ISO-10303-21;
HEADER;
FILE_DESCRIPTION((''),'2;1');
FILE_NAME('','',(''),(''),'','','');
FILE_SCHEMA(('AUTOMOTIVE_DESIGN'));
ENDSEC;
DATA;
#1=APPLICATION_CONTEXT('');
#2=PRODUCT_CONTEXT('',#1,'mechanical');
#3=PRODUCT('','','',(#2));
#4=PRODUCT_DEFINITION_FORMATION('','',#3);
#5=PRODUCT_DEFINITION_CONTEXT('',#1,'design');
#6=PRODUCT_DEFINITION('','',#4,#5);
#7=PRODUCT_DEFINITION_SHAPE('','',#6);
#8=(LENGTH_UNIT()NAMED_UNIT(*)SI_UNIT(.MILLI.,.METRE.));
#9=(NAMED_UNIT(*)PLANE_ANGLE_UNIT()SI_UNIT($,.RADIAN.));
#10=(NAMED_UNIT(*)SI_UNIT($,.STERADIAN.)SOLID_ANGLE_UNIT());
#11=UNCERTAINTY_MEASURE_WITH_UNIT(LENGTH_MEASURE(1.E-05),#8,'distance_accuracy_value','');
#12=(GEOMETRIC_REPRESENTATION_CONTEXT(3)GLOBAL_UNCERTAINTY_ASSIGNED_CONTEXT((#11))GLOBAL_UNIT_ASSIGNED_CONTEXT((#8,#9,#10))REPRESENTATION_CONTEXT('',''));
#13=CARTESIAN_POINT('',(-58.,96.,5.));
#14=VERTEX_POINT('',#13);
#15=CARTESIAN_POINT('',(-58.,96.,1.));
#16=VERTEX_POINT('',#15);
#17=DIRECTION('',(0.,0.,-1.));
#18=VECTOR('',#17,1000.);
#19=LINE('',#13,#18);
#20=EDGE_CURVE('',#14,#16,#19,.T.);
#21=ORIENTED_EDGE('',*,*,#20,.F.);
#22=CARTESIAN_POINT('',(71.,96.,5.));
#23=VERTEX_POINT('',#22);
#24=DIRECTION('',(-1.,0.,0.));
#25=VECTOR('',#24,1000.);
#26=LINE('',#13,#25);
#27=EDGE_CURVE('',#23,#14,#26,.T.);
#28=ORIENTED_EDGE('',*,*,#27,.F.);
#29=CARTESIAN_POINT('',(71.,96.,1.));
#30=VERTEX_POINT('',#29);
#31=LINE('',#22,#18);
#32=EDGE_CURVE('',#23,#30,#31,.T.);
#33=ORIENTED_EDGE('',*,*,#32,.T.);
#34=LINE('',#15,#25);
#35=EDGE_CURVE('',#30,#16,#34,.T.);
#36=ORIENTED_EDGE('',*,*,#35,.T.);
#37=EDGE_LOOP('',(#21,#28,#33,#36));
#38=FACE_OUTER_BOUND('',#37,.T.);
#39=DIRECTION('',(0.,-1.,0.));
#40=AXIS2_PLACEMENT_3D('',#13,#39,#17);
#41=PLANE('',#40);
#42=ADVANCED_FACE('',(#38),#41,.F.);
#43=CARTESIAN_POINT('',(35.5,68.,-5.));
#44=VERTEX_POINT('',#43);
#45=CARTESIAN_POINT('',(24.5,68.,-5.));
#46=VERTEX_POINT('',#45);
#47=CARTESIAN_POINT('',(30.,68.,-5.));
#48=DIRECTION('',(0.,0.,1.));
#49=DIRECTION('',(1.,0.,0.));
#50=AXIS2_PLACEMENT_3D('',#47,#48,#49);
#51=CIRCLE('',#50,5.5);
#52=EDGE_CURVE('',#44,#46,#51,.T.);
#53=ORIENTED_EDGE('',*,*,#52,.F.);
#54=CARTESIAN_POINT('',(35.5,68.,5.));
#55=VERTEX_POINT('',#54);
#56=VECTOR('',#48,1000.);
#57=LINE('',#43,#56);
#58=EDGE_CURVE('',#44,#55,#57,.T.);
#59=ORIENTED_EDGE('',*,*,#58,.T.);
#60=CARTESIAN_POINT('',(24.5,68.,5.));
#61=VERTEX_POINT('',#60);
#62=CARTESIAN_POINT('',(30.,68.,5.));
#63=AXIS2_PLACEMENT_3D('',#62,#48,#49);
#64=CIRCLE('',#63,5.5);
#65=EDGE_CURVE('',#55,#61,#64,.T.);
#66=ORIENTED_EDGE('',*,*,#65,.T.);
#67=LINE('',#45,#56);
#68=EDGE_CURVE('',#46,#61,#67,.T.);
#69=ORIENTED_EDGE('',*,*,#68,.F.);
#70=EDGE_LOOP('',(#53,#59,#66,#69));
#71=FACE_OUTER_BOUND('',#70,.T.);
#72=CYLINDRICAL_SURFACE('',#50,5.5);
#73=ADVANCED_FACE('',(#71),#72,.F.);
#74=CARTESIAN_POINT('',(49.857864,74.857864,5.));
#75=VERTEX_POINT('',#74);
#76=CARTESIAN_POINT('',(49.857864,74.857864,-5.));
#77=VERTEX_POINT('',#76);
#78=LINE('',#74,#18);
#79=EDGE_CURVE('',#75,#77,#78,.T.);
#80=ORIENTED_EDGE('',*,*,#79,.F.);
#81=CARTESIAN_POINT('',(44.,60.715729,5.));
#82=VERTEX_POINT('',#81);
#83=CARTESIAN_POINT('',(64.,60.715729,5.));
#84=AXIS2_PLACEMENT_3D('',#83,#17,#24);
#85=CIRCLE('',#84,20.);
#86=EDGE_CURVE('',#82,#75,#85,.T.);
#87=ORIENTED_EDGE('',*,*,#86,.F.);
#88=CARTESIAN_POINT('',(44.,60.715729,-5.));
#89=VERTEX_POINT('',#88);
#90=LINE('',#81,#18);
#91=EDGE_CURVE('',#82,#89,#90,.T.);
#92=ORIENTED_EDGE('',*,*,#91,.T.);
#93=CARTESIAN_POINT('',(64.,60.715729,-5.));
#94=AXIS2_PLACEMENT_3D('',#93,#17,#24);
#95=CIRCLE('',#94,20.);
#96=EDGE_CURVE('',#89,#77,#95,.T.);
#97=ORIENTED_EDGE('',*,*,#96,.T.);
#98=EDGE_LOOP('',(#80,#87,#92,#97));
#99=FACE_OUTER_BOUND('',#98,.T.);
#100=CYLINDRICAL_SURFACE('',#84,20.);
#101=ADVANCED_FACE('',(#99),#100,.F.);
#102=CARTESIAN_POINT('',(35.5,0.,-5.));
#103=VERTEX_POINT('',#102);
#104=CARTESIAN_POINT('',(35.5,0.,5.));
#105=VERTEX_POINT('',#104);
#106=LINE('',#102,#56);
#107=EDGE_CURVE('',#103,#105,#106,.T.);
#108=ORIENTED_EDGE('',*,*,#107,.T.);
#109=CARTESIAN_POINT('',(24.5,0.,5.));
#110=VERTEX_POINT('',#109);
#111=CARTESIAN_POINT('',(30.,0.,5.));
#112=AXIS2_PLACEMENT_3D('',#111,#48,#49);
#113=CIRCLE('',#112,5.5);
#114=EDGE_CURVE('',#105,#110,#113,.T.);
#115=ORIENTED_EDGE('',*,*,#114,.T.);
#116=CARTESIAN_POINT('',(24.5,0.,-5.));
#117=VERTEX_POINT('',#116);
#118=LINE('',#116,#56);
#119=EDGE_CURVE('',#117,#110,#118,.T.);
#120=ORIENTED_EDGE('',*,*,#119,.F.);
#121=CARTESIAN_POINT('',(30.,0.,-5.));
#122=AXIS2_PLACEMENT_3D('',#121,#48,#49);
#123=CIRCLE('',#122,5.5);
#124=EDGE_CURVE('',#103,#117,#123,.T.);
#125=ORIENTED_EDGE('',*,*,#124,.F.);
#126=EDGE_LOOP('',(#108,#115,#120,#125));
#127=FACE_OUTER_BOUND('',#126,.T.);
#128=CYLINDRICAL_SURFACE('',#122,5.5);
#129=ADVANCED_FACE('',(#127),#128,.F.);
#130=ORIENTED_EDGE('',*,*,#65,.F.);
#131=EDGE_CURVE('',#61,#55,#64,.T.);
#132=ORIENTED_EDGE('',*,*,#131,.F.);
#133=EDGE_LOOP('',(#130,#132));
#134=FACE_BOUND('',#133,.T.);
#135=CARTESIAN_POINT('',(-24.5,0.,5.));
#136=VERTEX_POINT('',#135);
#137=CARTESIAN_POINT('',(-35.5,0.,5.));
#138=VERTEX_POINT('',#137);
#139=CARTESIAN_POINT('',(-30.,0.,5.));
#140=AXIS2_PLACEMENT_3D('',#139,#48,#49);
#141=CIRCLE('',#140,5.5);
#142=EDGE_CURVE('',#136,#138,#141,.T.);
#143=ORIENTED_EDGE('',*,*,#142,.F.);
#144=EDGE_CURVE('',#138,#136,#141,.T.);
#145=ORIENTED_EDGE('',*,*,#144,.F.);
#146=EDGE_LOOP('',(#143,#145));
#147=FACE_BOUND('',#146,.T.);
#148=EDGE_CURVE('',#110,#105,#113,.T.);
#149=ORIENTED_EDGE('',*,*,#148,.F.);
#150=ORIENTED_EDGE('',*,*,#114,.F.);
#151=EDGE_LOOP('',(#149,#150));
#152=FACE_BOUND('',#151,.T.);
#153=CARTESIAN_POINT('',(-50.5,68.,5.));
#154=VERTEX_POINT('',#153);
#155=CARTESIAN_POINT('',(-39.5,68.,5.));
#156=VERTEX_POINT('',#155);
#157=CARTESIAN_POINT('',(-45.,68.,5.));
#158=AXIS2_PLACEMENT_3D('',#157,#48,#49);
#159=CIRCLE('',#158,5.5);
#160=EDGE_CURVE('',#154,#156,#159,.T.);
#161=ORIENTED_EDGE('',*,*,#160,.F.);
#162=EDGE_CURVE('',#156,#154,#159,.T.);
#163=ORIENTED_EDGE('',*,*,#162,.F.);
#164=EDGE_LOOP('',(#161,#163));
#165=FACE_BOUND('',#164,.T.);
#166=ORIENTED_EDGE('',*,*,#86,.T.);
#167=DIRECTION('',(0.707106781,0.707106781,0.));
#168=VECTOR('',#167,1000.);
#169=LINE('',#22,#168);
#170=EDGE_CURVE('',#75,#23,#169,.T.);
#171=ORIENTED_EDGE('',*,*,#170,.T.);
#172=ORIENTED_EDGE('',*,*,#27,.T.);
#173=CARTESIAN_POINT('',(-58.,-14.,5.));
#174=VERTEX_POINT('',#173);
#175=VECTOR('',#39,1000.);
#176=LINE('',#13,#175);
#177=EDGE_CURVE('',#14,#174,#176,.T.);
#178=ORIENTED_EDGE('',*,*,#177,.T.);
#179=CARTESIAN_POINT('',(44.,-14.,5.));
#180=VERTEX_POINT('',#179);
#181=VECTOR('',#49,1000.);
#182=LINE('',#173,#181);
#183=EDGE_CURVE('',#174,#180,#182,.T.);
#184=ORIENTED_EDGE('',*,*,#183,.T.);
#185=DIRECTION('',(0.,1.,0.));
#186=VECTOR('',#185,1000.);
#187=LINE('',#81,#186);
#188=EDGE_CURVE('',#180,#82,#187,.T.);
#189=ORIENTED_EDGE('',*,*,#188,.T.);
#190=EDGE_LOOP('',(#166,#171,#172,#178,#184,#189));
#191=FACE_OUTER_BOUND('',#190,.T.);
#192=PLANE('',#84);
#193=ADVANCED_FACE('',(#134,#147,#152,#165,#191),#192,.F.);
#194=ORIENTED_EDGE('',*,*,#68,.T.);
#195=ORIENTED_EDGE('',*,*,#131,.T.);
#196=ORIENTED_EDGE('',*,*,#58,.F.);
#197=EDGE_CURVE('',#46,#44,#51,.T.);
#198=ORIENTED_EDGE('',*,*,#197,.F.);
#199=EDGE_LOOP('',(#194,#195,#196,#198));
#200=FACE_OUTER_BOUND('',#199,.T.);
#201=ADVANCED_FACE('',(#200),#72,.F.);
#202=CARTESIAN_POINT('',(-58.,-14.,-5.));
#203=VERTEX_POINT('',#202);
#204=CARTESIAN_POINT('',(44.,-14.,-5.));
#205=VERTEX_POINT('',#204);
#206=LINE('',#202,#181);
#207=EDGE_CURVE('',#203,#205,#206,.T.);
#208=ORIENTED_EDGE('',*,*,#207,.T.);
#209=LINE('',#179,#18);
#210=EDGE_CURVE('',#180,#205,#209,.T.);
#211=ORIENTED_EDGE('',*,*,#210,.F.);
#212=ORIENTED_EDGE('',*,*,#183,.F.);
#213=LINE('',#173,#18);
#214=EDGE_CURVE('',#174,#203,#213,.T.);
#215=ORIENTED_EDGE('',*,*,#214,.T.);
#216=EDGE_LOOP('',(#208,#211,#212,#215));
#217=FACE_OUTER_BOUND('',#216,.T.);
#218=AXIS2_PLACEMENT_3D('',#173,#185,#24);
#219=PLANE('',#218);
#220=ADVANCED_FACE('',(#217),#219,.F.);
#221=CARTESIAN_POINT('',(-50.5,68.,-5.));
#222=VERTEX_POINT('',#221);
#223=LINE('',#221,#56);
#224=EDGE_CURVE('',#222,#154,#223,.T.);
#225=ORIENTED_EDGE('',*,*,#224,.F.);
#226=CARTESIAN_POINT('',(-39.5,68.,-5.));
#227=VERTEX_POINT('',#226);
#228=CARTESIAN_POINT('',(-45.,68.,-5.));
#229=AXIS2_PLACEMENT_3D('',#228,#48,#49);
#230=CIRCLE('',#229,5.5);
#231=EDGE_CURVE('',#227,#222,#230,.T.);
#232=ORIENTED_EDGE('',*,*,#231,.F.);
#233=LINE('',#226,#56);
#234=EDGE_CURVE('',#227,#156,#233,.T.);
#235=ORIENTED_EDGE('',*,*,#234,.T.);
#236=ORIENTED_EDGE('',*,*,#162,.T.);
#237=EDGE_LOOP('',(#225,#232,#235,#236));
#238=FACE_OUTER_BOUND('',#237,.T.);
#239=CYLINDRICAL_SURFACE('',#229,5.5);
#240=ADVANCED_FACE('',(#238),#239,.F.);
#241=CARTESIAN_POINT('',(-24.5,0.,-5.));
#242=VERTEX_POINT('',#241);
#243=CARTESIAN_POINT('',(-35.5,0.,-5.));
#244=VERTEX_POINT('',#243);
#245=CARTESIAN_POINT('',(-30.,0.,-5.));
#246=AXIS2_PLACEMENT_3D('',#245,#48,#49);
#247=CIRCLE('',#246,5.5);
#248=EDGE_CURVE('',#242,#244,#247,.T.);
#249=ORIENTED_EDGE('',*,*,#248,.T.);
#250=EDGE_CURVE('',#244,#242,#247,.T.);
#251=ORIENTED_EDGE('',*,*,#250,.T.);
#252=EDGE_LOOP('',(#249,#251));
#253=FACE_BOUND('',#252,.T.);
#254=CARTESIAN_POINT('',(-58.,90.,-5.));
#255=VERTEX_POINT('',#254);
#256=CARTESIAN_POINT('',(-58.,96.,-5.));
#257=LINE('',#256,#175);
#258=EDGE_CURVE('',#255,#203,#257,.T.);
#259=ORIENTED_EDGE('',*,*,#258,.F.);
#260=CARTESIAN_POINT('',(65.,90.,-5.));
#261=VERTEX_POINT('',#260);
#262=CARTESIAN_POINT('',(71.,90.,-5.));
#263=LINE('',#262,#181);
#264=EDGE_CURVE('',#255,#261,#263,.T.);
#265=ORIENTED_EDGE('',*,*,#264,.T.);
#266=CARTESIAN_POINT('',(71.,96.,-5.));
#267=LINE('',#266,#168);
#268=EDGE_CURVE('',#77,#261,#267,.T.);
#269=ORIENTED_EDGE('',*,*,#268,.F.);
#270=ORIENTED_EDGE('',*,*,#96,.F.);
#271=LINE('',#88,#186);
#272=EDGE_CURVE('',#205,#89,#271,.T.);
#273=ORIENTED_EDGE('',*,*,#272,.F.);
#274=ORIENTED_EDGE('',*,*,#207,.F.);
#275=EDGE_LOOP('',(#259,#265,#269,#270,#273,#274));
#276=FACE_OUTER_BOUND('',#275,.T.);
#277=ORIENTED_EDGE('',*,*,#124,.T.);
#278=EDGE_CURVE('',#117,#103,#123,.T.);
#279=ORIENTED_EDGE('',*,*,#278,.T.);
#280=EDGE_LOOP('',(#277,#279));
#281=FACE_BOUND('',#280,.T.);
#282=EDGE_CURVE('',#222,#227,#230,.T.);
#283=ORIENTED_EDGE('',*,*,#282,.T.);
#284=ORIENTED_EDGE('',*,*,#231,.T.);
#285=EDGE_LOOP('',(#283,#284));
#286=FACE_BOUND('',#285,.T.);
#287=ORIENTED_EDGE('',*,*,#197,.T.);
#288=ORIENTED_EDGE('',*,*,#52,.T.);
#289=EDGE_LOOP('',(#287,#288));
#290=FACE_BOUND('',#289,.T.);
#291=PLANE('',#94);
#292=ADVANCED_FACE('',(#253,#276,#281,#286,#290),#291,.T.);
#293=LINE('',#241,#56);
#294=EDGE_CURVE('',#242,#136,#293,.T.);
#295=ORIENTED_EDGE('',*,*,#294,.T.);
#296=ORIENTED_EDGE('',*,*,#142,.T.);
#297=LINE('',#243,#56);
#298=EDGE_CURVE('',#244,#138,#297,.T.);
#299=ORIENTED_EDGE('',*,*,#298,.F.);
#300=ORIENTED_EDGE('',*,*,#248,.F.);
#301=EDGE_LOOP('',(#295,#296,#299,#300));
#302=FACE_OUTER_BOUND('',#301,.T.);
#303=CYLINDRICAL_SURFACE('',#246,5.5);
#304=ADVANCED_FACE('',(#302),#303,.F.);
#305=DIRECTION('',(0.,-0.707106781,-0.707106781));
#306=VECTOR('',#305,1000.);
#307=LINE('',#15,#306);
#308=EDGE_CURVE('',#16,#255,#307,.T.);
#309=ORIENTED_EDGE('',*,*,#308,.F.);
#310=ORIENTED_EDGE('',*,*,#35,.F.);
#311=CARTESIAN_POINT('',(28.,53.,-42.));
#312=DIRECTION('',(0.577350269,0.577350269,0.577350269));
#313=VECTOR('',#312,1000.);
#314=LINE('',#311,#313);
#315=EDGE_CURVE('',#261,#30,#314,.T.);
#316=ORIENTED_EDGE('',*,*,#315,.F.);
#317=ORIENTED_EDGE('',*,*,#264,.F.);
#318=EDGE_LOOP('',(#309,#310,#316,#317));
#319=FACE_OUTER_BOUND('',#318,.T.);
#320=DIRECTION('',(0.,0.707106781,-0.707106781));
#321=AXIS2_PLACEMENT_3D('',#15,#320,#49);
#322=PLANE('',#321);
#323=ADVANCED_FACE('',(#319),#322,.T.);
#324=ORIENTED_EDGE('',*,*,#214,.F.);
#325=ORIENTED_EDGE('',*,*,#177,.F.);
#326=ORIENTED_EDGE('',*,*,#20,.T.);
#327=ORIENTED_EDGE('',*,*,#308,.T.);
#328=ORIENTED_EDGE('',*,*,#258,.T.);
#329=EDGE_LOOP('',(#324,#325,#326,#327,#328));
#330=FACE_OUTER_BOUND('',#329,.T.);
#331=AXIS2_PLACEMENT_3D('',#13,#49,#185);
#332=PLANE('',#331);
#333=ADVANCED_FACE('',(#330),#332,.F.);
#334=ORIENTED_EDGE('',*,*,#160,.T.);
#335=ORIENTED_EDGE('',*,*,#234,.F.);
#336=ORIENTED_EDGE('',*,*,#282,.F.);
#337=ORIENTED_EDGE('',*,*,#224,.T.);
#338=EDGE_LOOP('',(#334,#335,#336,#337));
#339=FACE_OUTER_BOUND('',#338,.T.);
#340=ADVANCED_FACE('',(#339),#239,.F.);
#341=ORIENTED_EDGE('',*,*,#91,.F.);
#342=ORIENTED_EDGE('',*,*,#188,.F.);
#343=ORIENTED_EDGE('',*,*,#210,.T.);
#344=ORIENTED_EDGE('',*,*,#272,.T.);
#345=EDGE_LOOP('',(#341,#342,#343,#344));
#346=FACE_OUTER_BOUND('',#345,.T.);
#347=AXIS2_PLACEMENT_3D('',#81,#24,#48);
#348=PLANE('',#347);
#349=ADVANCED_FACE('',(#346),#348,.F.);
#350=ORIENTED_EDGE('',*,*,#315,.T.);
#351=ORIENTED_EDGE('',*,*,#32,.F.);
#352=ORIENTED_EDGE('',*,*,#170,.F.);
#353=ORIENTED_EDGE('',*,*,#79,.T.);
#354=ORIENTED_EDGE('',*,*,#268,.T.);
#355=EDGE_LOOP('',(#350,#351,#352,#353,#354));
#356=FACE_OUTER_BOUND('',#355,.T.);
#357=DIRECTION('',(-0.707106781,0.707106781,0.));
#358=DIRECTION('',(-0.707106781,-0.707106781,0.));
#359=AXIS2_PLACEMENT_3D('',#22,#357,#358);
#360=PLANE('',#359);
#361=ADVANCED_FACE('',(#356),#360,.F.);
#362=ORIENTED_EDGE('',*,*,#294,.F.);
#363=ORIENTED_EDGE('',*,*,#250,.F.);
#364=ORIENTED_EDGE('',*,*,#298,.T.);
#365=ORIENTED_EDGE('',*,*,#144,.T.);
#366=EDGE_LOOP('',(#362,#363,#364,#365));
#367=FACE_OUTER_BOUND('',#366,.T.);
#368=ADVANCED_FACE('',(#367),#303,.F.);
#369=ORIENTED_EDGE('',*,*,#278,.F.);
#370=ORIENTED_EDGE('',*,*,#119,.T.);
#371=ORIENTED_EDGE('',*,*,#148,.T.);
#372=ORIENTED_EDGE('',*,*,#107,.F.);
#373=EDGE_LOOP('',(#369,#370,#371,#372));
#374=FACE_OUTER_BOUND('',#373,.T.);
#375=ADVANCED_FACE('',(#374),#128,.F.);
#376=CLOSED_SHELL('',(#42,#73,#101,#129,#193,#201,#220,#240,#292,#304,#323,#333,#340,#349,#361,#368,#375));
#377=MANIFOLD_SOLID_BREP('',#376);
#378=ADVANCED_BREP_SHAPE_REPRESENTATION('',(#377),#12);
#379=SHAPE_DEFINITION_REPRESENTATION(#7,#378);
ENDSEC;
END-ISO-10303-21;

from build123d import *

# Parameters (mm, degrees)
BOSS_EXTRUDE1_DEPTH     = 5
CUT_EXTRUDE1_DEPTH      = 120.507321951
CUT_EXTRUDE1_DEPTH_BACK = 120.507321951
SKETCH2_R               = 5.5
CHAMFER1_SIZE           = 6


with BuildPart() as part:
    # Sketch1 → Boss-Extrude1 (new, symmetric)
    with BuildSketch(Plane.XY):
        with BuildLine():
            Line((-58, 96), (71, 96))
            Line((71, 96), (49.857864376, 74.857864376))
            ThreePointArc((49.857864376, 74.857864376), (45.52240935, 68.3693974), (44, 60.715728753))
            Line((44, 60.715728753), (44, -14))
            Line((44, -14), (-58, -14))
            Line((-58, -14), (-58, 96))
        make_face()
    extrude(amount=BOSS_EXTRUDE1_DEPTH, both=True)

    # Sketch2 → Cut-Extrude1 (cut, two sides: drawn at the far end of the back side and taken through both)
    with BuildSketch(Plane.XY.offset(-CUT_EXTRUDE1_DEPTH_BACK)):
        with Locations((-30, 0)):
            Circle(SKETCH2_R)
        with Locations((30, 0)):
            Circle(SKETCH2_R)
        with Locations((-45, 68)):
            Circle(SKETCH2_R)
        with Locations((30, 68)):
            Circle(SKETCH2_R)
    extrude(amount=CUT_EXTRUDE1_DEPTH + CUT_EXTRUDE1_DEPTH_BACK, mode=Mode.SUBTRACT)

    # Chamfer1
    chamfer1_edges = [part.edges().sort_by_distance(p)[0] for p in [
        (6.5, 96, -5),
    ]]
    chamfer(chamfer1_edges, length=CHAMFER1_SIZE)


solid = part.part
